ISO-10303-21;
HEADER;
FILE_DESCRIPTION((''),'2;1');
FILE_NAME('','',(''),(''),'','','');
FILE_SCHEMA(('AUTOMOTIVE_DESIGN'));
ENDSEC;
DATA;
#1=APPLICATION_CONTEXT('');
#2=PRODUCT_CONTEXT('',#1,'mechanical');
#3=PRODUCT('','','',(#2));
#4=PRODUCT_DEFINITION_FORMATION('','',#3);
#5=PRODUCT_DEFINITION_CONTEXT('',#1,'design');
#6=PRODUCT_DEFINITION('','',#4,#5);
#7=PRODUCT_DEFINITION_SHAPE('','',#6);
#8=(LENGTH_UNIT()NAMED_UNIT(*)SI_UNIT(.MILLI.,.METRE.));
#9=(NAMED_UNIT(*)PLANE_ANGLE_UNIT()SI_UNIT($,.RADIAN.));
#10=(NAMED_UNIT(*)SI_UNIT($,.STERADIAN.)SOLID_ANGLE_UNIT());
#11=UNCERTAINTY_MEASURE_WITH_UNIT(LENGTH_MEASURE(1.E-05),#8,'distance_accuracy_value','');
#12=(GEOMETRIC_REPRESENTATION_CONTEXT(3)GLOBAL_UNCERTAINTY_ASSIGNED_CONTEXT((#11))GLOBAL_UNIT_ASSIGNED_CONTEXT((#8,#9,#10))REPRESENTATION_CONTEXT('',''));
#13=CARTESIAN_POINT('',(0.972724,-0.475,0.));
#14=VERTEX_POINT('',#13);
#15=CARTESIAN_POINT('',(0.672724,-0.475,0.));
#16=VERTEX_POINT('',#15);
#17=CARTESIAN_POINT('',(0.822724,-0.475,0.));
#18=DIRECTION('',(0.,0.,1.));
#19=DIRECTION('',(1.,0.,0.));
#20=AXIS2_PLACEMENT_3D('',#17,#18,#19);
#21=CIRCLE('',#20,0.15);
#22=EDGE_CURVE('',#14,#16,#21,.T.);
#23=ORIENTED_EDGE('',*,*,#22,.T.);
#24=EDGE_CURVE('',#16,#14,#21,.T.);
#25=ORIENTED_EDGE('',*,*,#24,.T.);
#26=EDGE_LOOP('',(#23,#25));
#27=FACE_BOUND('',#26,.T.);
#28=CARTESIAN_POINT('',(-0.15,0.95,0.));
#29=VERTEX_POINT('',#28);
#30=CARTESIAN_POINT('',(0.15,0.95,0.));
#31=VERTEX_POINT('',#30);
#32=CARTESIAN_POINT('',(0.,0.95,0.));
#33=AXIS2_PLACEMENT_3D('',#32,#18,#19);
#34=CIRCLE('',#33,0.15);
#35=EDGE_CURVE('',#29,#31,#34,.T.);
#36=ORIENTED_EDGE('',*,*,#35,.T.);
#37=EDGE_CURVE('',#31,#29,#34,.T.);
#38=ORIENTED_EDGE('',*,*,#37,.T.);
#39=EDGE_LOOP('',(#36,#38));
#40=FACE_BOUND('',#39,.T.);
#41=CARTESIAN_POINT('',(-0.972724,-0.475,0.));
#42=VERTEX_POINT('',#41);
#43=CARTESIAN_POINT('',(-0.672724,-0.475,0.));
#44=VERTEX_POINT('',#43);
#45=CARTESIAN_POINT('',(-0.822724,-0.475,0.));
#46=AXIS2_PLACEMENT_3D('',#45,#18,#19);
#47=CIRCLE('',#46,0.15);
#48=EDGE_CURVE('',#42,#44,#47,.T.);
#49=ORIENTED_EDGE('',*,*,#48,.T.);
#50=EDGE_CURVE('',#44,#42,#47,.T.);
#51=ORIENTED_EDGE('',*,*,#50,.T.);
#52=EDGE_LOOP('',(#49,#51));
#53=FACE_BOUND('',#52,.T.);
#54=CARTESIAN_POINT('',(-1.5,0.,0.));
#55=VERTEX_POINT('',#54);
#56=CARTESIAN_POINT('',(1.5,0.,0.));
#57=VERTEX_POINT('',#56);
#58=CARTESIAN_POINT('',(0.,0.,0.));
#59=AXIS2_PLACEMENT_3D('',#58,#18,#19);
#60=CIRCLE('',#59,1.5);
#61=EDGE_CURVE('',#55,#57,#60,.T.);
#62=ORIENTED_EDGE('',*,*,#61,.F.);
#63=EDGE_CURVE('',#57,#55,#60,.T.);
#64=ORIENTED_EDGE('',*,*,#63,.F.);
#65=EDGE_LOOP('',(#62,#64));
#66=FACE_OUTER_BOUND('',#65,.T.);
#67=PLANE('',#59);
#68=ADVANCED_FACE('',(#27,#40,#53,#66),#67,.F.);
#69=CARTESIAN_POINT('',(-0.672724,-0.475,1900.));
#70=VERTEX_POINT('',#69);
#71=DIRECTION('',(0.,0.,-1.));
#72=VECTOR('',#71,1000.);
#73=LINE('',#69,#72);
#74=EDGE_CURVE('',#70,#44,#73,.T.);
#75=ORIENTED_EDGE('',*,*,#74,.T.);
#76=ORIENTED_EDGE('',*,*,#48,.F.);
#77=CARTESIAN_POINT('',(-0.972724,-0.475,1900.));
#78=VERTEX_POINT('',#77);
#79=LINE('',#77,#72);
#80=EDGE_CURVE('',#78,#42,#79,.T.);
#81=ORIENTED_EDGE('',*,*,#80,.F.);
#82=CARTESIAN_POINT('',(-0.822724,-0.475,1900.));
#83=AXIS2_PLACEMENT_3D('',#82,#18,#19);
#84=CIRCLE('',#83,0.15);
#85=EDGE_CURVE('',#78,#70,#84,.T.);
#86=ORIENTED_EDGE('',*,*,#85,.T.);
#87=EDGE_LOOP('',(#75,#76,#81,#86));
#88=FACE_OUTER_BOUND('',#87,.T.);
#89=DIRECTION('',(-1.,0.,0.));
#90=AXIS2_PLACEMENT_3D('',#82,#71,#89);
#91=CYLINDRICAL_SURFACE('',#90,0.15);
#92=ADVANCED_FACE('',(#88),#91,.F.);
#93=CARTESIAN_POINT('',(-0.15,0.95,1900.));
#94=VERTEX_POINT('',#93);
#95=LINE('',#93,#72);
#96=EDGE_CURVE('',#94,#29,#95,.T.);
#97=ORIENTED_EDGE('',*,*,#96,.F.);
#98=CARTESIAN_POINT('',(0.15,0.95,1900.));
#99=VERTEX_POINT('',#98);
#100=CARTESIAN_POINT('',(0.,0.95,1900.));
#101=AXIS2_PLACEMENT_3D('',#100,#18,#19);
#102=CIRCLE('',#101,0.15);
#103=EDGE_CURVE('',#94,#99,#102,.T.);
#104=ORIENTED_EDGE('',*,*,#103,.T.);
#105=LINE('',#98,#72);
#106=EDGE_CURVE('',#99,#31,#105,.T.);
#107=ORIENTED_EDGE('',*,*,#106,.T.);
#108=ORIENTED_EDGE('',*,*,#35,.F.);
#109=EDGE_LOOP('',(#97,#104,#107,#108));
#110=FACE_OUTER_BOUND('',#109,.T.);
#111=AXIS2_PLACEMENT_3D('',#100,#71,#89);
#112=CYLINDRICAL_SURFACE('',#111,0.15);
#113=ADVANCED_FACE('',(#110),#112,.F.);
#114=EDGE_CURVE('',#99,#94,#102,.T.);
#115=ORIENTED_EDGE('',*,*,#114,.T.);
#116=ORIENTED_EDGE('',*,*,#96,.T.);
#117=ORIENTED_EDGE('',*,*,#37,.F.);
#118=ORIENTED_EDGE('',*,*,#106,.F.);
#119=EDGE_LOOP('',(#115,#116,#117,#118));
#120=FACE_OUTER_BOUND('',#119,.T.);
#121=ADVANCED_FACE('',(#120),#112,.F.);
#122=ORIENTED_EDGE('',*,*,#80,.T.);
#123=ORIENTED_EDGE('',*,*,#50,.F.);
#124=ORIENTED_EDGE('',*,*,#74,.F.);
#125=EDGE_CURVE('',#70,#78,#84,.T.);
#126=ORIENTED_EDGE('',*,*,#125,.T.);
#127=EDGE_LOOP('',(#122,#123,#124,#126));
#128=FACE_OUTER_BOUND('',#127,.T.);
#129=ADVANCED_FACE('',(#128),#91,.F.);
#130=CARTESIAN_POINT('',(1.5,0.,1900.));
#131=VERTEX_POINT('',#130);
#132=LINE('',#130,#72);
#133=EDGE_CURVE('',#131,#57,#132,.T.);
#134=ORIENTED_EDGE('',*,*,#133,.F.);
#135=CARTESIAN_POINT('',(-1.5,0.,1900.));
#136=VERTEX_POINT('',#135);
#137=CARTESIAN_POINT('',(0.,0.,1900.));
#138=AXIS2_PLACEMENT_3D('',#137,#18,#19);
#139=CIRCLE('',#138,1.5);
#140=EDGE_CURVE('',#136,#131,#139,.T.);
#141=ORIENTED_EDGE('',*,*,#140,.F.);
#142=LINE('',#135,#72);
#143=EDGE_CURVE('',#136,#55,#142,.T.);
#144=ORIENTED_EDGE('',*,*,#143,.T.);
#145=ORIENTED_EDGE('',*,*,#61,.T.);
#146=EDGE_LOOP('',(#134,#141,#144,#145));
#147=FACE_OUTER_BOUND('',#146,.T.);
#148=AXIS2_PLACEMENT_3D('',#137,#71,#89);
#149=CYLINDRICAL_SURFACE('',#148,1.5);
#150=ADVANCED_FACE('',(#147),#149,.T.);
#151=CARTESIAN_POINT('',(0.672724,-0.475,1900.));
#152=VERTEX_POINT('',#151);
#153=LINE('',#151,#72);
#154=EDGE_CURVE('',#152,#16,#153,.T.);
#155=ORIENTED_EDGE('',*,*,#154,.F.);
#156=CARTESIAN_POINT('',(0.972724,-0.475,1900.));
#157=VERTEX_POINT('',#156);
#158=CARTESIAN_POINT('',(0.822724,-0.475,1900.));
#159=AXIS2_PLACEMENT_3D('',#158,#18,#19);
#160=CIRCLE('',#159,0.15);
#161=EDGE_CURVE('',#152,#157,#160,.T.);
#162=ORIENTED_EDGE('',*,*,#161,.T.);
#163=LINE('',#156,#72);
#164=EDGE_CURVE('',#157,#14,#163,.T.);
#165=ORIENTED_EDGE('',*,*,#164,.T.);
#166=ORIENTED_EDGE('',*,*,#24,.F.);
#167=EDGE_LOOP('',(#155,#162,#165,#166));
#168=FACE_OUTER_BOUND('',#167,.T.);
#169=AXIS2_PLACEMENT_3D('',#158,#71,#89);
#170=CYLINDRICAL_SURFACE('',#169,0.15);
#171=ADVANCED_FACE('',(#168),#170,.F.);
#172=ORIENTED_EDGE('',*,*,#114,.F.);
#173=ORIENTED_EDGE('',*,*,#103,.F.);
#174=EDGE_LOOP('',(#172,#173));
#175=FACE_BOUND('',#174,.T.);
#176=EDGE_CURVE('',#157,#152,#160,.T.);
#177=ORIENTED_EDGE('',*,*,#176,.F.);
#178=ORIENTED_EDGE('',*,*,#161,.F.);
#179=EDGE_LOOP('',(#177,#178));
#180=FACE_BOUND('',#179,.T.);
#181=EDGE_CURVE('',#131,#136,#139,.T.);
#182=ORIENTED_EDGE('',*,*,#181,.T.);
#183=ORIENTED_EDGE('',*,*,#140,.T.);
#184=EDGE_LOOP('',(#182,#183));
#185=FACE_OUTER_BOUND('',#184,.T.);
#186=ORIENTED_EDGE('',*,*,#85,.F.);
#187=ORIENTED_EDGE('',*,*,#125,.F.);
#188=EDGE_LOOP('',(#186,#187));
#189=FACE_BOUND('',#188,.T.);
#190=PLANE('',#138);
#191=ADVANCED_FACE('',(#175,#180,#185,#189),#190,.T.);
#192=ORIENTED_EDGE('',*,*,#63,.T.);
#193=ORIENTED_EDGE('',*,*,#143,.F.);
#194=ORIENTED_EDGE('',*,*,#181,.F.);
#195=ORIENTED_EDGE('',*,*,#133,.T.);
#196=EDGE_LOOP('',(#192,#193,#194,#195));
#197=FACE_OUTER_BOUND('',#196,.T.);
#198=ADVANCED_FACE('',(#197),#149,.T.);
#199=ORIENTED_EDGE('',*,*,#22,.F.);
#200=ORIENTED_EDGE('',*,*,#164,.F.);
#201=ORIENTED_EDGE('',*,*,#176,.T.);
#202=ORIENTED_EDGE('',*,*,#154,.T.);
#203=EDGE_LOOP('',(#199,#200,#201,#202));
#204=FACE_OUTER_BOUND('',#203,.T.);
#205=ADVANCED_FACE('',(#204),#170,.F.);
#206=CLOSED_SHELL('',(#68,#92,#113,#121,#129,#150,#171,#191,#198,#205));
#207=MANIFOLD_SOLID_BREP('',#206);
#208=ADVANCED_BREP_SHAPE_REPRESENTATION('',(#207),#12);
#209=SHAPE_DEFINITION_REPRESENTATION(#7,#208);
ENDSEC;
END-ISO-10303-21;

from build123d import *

# Parameters (mm, degrees)
SKETCH1_R           = 1.5
SKETCH1_R_2         = 0.15
BOSS_EXTRUDE1_DEPTH = 1900


with BuildPart() as part:
    # Sketch1 → Boss-Extrude1 (new body)
    with BuildSketch(Plane.XY):
        with Locations(Location((0, 0, 0), (0, 0, 180))):
            Circle(SKETCH1_R)
        with Locations((0, 0.95)):
            Circle(SKETCH1_R_2, mode=Mode.SUBTRACT)
        with Locations((0.822724134, -0.475)):
            Circle(SKETCH1_R_2, mode=Mode.SUBTRACT)
        with Locations((-0.822724134, -0.475)):
            Circle(SKETCH1_R_2, mode=Mode.SUBTRACT)
    extrude(amount=BOSS_EXTRUDE1_DEPTH)


solid = part.part
